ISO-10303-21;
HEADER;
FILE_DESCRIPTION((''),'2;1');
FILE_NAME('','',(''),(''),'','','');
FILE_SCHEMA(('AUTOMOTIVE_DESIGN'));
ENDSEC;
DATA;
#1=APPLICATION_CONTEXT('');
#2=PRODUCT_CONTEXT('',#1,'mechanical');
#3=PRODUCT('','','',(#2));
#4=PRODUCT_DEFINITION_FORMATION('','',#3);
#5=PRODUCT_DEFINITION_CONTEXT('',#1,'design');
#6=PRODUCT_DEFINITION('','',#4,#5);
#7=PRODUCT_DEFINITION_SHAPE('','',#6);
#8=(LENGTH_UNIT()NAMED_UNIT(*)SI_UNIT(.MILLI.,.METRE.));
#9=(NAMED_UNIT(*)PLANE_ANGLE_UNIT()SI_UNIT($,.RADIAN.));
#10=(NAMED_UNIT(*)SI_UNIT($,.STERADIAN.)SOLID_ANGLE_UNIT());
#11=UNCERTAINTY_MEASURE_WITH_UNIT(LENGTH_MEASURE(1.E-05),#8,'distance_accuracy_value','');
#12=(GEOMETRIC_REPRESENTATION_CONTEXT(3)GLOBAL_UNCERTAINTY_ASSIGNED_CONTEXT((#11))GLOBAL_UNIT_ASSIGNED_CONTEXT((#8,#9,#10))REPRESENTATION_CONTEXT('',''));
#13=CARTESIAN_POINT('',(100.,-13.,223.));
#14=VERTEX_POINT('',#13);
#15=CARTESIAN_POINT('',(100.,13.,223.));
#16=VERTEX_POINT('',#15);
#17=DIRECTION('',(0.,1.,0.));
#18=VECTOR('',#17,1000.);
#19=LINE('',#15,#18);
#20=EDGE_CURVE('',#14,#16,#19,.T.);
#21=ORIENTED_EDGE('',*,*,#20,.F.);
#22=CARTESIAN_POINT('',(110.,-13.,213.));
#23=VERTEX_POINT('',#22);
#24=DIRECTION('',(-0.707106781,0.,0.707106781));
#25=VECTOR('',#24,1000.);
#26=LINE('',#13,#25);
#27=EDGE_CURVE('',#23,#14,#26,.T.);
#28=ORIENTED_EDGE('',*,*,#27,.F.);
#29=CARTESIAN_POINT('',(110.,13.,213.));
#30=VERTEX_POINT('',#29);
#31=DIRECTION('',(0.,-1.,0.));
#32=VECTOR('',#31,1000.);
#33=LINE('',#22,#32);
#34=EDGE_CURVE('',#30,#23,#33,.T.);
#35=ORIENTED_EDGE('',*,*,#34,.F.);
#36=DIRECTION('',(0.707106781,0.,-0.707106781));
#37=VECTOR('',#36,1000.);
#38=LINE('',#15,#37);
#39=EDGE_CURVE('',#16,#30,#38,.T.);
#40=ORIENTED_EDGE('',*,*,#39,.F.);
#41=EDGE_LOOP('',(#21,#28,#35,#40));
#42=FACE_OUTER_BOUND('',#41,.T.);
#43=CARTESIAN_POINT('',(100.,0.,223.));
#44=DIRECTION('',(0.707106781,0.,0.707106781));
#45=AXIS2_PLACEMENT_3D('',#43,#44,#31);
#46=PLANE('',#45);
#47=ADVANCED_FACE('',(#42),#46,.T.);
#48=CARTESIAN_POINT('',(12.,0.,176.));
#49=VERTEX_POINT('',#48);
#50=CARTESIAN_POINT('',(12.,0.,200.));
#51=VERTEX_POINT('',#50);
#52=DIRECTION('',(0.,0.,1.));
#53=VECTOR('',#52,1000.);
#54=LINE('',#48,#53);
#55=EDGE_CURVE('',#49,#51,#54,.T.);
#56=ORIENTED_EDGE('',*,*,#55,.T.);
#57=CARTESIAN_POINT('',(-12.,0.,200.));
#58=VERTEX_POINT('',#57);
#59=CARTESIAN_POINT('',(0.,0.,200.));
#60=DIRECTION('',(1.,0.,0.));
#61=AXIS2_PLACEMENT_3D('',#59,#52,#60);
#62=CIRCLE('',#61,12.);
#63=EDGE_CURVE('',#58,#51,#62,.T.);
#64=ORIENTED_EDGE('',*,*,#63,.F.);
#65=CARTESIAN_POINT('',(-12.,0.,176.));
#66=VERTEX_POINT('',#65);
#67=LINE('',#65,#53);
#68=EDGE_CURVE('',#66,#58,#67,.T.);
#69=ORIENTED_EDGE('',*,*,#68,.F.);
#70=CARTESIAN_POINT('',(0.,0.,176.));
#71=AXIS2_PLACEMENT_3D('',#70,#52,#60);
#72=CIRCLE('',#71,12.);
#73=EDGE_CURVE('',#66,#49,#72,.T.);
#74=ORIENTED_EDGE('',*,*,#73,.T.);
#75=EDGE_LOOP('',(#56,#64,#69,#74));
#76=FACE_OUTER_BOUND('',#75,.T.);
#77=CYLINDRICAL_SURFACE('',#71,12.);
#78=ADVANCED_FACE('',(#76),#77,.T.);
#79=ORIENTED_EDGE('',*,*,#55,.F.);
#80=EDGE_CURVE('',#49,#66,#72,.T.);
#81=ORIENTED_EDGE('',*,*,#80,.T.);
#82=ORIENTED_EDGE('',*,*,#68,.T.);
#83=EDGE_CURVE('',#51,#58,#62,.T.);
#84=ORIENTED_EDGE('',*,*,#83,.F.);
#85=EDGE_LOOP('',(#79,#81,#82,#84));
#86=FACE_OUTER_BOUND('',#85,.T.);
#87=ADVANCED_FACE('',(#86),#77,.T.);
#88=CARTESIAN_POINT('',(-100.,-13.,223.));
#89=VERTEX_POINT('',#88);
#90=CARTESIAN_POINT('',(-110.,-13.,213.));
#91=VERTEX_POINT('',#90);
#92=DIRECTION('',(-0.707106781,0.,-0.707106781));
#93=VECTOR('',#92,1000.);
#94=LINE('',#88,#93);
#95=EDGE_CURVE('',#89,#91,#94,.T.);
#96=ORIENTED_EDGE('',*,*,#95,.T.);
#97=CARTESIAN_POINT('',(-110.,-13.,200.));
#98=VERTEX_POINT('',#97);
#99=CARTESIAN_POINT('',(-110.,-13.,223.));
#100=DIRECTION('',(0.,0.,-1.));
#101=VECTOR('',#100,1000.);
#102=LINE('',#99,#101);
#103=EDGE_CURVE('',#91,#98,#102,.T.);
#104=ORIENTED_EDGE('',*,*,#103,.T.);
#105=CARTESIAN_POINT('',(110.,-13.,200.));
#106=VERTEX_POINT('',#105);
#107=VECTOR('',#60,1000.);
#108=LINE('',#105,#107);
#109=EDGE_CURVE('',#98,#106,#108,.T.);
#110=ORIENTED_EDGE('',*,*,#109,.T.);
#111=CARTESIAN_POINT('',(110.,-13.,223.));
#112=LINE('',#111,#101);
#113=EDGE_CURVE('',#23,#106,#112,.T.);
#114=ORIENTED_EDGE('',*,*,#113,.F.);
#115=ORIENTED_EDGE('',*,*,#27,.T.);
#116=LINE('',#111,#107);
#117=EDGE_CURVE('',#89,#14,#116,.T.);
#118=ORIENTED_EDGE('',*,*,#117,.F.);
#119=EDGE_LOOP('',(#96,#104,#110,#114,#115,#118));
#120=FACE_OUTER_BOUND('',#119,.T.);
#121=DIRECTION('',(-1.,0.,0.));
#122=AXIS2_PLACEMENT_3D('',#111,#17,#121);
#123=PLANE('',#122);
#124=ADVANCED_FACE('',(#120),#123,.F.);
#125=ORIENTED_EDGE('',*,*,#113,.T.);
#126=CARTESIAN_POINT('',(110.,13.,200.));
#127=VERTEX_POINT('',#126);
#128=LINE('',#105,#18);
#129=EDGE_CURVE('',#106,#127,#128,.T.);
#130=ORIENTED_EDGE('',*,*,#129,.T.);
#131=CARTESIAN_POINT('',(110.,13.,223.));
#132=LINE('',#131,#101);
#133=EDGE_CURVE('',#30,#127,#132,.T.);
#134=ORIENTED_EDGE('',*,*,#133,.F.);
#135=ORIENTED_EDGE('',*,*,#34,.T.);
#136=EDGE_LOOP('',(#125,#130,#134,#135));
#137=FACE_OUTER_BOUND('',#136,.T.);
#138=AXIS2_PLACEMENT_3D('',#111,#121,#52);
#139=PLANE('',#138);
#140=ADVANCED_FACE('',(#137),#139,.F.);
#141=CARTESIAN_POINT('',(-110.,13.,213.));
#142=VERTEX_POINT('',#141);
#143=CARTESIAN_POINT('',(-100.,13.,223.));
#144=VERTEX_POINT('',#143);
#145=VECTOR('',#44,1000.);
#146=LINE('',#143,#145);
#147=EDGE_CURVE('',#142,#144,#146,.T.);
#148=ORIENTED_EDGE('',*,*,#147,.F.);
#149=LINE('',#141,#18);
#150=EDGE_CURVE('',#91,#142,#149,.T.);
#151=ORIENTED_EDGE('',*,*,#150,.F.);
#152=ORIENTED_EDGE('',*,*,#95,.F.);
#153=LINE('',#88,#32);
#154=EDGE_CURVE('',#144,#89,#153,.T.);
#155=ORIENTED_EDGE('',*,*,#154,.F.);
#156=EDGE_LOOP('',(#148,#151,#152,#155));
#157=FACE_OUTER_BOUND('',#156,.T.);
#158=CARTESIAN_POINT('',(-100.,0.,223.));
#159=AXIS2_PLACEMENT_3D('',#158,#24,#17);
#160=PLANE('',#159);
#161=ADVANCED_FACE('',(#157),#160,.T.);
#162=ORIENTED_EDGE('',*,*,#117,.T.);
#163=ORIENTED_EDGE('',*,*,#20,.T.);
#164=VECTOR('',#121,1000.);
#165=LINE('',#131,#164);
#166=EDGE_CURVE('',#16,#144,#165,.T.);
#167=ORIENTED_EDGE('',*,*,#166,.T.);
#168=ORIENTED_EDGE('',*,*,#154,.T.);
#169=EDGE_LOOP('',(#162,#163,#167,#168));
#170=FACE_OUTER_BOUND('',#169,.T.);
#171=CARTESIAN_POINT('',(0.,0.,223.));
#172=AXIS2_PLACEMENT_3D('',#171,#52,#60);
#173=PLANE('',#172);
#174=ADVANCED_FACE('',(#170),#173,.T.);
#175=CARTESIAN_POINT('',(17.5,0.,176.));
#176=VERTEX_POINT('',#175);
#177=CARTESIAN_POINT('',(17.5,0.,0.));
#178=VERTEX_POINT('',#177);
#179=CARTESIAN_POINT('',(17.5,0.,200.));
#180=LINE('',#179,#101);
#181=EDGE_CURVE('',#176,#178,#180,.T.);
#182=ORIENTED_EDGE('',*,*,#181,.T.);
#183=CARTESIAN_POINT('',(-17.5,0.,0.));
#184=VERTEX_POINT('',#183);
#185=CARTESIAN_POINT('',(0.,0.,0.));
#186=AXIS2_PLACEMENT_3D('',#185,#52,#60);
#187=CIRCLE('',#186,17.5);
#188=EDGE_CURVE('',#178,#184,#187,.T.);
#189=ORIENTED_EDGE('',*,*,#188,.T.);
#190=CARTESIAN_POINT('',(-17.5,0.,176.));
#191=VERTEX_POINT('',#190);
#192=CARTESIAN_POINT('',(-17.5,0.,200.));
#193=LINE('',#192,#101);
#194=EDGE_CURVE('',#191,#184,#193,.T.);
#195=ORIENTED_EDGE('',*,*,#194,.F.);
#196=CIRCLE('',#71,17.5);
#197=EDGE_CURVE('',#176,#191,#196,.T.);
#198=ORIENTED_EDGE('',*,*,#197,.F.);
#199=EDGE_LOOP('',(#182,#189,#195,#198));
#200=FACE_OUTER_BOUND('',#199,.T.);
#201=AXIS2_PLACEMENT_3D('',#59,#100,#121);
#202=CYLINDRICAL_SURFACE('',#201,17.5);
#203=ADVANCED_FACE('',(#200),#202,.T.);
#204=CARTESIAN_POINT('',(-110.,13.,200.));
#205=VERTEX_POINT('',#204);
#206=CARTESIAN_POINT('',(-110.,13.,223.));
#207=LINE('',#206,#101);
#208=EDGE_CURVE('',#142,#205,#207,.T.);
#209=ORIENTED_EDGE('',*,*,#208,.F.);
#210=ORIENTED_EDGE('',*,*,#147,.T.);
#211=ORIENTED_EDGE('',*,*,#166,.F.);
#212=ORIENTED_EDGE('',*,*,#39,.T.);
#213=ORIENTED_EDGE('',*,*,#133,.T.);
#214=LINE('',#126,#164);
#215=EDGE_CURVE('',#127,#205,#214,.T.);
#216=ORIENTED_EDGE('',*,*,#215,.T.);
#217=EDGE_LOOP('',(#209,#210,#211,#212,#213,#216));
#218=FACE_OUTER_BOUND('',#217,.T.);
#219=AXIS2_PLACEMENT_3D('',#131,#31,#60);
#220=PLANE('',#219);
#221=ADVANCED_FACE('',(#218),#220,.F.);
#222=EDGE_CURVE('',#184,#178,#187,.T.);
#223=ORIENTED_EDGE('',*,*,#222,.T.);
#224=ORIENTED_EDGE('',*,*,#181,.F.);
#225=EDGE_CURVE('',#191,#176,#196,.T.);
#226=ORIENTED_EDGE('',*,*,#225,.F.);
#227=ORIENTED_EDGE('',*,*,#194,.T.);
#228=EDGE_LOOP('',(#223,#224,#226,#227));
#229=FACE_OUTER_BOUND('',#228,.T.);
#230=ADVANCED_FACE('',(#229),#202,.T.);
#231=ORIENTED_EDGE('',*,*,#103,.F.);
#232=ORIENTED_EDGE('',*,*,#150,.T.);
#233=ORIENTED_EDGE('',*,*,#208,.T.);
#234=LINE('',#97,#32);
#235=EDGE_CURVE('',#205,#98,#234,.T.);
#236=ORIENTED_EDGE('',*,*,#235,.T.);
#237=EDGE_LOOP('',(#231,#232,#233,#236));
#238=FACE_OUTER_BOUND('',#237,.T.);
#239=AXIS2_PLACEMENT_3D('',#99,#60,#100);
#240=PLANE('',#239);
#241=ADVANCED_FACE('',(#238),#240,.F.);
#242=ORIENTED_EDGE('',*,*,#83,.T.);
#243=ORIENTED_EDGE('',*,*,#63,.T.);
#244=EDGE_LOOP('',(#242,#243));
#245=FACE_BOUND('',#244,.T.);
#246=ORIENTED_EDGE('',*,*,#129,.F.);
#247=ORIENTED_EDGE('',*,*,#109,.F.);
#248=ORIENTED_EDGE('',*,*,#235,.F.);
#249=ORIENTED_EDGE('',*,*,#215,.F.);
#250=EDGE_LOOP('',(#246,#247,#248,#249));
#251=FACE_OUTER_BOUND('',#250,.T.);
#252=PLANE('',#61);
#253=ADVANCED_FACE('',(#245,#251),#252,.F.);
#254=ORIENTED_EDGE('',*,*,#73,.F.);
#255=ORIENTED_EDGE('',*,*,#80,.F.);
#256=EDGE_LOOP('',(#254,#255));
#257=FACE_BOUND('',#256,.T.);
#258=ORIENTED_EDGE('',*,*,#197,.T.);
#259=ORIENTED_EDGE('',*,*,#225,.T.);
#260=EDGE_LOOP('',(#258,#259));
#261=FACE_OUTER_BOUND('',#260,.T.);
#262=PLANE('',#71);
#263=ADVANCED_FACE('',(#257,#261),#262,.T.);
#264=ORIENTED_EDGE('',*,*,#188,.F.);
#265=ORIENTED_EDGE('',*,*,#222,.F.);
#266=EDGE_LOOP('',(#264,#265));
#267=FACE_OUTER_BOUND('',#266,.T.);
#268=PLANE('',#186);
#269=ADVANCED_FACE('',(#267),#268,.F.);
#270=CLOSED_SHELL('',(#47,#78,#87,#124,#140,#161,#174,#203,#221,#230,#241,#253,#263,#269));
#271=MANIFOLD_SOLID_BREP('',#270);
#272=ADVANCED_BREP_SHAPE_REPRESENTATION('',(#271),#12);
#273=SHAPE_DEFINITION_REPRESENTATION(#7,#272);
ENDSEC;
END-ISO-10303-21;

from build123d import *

# Parameters (mm, degrees)
SKETCH1_R           = 17.5
BOSS_EXTRUDE1_DEPTH = 200
SKETCH3_OUTSIDE_W   = 78.206
SKETCH3_OUTSIDE_H   = 78.206
SKETCH3_OUTSIDE_R   = 12
CUT_EXTRUDE1_DEPTH  = 24
SKETCH4_W           = 220
SKETCH4_H           = 26
BOSS_EXTRUDE2_DEPTH = 23
CHAMFER1_SIZE       = 10


with BuildPart() as part:
    # Sketch1 → Boss-Extrude1 (new body)
    with BuildSketch(Plane.XY):
        Circle(SKETCH1_R)
    extrude(amount=BOSS_EXTRUDE1_DEPTH)

    # Sketch3 outside → Cut-Extrude1 (cut)
    with BuildSketch(Plane.XY.offset(200)):
        Rectangle(SKETCH3_OUTSIDE_W, SKETCH3_OUTSIDE_H)
        Circle(SKETCH3_OUTSIDE_R, mode=Mode.SUBTRACT)
    extrude(amount=-CUT_EXTRUDE1_DEPTH, mode=Mode.SUBTRACT)

    # Sketch4 → Boss-Extrude2 (add)
    with BuildSketch(Plane.XY.offset(200)):
        Rectangle(SKETCH4_W, SKETCH4_H)
    extrude(amount=BOSS_EXTRUDE2_DEPTH)

    # Chamfer1
    chamfer1_edges = [part.edges().sort_by_distance(p)[0] for p in [
        (-110, 0, 223),
        (110, 0, 223),
    ]]
    chamfer(chamfer1_edges, length=CHAMFER1_SIZE)


solid = part.part
